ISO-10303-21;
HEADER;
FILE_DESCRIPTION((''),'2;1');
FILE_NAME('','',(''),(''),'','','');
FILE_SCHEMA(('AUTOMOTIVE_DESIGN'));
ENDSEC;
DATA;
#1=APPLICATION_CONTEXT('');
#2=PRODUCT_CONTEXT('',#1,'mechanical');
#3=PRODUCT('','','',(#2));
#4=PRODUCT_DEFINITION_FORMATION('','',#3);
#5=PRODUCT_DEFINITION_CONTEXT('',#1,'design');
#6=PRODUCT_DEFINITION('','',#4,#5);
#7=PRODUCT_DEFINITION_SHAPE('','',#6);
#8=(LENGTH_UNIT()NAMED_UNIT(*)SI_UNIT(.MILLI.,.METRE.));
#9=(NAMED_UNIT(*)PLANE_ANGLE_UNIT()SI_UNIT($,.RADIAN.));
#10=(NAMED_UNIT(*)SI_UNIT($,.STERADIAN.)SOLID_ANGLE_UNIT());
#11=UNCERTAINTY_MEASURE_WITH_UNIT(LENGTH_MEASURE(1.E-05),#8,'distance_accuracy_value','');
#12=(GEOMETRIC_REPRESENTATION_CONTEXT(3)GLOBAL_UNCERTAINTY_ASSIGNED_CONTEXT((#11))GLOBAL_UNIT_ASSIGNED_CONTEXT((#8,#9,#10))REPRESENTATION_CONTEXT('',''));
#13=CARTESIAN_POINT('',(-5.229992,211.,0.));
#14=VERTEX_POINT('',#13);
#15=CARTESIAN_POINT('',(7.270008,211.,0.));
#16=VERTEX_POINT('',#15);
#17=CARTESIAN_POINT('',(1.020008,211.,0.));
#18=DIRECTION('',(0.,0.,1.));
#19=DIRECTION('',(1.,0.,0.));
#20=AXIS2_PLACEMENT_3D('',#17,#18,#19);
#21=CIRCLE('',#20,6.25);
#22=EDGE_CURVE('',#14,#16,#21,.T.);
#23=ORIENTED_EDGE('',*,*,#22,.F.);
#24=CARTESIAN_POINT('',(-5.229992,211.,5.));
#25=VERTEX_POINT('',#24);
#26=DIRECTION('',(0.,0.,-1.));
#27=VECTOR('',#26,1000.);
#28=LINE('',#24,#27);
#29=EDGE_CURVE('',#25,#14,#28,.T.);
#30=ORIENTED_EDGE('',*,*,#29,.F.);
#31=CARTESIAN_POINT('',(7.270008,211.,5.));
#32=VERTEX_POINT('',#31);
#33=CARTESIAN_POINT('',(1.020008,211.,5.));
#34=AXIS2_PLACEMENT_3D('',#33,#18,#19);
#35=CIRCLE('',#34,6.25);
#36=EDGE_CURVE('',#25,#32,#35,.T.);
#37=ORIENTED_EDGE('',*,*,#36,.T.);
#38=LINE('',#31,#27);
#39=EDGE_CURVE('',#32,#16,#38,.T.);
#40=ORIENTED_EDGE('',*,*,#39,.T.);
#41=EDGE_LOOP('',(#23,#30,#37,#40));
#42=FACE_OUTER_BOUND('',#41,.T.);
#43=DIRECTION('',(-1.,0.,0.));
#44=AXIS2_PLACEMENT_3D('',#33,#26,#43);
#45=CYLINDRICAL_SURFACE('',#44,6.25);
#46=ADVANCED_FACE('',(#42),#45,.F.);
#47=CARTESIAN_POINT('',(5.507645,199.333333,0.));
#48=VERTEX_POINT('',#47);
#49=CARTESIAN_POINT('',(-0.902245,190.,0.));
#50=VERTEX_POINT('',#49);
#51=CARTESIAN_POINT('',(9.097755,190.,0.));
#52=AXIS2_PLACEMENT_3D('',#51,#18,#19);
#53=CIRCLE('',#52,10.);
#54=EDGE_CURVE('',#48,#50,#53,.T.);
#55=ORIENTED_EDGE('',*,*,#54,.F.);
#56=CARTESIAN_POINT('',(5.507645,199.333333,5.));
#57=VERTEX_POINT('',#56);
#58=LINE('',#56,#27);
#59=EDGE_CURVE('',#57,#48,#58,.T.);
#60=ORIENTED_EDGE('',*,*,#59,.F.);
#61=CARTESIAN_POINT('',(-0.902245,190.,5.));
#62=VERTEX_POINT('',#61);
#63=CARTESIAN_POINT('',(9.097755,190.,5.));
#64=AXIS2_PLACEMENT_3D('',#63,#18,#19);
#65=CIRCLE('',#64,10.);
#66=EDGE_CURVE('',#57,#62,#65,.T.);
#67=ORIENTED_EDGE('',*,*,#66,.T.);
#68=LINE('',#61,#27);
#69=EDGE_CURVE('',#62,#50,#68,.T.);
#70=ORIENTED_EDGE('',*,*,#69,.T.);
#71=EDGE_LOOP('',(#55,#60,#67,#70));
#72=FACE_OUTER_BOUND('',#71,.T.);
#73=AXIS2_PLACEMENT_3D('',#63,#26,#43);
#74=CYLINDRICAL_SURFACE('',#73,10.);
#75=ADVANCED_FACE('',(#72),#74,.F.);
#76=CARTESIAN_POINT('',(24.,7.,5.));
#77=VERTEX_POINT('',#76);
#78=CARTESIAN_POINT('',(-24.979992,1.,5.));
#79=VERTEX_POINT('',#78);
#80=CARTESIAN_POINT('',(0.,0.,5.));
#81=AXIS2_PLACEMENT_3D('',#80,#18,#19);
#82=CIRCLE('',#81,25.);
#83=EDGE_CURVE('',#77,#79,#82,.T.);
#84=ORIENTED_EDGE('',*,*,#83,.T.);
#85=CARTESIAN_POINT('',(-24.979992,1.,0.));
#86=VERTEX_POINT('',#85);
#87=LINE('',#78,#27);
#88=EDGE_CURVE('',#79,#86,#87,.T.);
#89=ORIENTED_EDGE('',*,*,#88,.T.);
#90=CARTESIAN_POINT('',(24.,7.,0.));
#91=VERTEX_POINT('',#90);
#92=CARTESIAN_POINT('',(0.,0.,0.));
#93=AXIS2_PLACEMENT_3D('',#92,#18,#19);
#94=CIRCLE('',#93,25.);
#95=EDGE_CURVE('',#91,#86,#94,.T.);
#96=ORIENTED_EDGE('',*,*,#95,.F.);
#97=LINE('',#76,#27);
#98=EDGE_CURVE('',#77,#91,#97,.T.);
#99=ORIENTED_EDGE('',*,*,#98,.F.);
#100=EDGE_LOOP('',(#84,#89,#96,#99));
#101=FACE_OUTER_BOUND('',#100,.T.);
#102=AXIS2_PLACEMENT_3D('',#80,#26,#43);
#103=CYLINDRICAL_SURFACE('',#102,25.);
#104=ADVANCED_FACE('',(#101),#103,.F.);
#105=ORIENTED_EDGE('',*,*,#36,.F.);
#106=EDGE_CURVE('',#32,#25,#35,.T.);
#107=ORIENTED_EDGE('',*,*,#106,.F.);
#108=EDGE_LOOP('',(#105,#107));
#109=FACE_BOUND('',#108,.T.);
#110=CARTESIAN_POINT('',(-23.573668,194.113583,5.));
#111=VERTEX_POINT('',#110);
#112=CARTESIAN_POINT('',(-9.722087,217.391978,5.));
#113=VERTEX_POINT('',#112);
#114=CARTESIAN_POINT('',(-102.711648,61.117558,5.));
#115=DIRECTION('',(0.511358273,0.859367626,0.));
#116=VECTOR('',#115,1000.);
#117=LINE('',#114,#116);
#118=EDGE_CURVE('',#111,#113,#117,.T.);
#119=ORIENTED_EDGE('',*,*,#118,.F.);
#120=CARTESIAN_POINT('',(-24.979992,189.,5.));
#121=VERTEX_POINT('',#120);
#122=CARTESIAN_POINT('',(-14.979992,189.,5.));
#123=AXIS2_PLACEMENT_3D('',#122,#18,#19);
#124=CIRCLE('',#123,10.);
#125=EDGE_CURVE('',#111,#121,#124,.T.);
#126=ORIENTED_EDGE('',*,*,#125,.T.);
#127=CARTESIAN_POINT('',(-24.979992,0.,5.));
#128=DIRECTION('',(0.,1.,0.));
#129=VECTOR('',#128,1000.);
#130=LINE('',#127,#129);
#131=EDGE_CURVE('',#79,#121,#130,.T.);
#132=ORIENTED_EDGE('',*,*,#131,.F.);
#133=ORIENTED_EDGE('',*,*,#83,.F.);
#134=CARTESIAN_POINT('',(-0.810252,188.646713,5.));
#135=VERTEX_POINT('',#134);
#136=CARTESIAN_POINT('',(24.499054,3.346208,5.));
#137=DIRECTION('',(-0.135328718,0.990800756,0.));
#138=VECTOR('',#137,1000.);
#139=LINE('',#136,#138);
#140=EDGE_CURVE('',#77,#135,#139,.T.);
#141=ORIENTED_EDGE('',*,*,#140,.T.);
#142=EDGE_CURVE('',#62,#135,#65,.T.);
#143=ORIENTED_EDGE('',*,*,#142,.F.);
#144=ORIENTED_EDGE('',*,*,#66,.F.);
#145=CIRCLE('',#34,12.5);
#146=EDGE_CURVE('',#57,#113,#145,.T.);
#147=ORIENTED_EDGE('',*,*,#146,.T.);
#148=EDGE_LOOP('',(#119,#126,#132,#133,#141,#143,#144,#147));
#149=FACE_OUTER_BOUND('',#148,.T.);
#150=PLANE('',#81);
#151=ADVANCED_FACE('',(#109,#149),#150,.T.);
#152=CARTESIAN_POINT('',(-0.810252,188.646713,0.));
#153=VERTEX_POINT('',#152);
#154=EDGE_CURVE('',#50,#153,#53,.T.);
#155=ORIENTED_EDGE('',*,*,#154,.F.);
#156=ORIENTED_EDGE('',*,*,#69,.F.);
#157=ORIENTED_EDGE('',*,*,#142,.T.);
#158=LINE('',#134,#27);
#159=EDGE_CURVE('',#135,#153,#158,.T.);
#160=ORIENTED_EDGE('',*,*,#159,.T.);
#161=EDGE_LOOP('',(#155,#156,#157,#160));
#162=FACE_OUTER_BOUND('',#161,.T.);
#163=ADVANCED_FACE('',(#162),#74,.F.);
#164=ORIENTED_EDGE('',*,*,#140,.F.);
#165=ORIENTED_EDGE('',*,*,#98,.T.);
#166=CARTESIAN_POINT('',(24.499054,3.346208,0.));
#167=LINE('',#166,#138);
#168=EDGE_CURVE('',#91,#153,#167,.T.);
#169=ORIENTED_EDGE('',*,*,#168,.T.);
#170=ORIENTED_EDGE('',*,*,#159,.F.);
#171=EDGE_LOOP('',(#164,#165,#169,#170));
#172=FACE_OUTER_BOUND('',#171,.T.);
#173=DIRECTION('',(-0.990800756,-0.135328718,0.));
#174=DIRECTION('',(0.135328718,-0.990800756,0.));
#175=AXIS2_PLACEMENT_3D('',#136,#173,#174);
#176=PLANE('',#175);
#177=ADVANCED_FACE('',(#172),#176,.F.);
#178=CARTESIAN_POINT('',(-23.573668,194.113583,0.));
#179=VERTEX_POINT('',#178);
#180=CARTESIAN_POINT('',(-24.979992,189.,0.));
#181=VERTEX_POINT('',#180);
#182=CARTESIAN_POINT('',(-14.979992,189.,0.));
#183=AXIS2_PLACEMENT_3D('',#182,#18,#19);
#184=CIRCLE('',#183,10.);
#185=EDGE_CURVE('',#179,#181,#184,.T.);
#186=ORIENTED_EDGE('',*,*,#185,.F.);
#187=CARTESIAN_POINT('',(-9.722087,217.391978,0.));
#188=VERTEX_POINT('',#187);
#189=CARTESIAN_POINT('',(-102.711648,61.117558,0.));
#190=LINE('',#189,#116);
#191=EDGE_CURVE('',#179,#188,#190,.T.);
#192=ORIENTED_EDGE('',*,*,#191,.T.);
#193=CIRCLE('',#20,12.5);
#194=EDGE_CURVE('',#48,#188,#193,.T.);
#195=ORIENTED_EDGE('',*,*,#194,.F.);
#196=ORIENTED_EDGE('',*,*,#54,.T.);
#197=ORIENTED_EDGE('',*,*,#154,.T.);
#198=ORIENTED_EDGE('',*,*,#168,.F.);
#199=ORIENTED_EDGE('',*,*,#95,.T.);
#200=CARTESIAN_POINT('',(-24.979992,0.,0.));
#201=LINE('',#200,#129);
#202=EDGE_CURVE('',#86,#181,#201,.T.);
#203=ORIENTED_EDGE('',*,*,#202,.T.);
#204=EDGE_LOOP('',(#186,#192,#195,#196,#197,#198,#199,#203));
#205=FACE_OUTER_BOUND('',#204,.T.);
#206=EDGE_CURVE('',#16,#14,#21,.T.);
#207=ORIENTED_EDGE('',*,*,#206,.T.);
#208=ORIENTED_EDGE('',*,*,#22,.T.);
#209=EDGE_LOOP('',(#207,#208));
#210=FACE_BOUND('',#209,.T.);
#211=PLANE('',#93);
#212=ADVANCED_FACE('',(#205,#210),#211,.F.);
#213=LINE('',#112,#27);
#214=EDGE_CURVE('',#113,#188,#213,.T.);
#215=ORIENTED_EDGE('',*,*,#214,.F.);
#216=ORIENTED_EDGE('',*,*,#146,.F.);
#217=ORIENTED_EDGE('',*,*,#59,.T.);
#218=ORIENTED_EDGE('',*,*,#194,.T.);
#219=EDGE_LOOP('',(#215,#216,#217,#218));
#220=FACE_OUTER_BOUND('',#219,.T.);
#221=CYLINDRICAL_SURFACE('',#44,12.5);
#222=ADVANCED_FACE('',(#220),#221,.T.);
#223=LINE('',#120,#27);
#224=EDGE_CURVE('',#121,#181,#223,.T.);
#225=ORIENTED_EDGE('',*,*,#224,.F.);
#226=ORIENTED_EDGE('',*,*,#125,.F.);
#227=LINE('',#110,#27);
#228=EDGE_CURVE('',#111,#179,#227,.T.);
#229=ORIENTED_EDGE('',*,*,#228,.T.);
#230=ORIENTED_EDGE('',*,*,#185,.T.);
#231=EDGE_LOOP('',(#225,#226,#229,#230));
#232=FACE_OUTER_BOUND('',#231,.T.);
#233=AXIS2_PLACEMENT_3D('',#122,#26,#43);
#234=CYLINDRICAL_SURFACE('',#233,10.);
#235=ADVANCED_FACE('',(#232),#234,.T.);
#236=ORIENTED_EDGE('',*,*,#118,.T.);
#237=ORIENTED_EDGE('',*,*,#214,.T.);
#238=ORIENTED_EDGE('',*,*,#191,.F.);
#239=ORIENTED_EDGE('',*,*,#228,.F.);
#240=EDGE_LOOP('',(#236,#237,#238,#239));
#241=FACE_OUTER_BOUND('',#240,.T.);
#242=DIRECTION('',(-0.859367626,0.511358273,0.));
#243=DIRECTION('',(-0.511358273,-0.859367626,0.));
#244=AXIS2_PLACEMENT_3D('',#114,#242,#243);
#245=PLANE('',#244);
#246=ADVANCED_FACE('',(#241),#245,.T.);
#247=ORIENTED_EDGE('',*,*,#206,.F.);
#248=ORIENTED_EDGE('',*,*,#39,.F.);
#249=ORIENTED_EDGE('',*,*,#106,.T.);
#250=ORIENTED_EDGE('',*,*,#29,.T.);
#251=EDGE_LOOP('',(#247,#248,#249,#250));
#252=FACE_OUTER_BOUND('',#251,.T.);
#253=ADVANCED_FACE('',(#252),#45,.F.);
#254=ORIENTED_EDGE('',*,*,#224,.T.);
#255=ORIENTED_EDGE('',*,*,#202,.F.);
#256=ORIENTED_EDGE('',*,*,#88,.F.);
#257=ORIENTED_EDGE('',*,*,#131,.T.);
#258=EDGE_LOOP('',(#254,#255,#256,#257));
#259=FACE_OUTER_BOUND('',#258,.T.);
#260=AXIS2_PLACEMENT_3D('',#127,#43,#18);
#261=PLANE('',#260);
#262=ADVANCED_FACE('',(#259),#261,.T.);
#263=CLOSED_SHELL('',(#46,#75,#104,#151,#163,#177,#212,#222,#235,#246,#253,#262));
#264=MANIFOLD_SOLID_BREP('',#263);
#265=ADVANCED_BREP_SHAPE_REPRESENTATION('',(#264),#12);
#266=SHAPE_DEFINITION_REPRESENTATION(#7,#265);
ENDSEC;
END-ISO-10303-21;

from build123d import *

# Parameters (mm, degrees)
SKETCH1_R           = 12.5
SKETCH1_R_2         = 6.25
BOSS_EXTRUDE1_DEPTH = 5


with BuildPart() as part:
    # Sketch1 → Boss-Extrude1 (new body)
    # profile 1 of 2: a face of its own
    with BuildSketch(Plane.XY):
        with BuildLine():
            Line((-24.979991994, 189), (-24.979991994, 1))
            ThreePointArc((-24.979991994, 1), (-3.039752634, 24.814509947), (24, 7))
            Line((24, 7), (-0.810252343, 188.64671282))
            ThreePointArc((-0.810252343, 188.64671282), (0.4895755, 195.089129783), (5.507645346, 199.333333333))
            ThreePointArc((5.507645346, 199.333333333), (-8.535525821, 202.941354129), (-9.722087316, 217.391978417))
            Line((-9.722087316, 217.391978417), (-23.573668252, 194.113582733))
            ThreePointArc((-23.573668252, 194.113582733), (-24.622003262, 191.651719953), (-24.979991994, 189))
        make_face()
    # profile 2 of 2: a face of its own
    with BuildSketch(Plane.XY):
        with Locations((1.020008006, 211)):
            Circle(SKETCH1_R)
        with Locations((1.020008006, 211)):
            Circle(SKETCH1_R_2, mode=Mode.SUBTRACT)
    extrude(amount=BOSS_EXTRUDE1_DEPTH)


solid = part.part
